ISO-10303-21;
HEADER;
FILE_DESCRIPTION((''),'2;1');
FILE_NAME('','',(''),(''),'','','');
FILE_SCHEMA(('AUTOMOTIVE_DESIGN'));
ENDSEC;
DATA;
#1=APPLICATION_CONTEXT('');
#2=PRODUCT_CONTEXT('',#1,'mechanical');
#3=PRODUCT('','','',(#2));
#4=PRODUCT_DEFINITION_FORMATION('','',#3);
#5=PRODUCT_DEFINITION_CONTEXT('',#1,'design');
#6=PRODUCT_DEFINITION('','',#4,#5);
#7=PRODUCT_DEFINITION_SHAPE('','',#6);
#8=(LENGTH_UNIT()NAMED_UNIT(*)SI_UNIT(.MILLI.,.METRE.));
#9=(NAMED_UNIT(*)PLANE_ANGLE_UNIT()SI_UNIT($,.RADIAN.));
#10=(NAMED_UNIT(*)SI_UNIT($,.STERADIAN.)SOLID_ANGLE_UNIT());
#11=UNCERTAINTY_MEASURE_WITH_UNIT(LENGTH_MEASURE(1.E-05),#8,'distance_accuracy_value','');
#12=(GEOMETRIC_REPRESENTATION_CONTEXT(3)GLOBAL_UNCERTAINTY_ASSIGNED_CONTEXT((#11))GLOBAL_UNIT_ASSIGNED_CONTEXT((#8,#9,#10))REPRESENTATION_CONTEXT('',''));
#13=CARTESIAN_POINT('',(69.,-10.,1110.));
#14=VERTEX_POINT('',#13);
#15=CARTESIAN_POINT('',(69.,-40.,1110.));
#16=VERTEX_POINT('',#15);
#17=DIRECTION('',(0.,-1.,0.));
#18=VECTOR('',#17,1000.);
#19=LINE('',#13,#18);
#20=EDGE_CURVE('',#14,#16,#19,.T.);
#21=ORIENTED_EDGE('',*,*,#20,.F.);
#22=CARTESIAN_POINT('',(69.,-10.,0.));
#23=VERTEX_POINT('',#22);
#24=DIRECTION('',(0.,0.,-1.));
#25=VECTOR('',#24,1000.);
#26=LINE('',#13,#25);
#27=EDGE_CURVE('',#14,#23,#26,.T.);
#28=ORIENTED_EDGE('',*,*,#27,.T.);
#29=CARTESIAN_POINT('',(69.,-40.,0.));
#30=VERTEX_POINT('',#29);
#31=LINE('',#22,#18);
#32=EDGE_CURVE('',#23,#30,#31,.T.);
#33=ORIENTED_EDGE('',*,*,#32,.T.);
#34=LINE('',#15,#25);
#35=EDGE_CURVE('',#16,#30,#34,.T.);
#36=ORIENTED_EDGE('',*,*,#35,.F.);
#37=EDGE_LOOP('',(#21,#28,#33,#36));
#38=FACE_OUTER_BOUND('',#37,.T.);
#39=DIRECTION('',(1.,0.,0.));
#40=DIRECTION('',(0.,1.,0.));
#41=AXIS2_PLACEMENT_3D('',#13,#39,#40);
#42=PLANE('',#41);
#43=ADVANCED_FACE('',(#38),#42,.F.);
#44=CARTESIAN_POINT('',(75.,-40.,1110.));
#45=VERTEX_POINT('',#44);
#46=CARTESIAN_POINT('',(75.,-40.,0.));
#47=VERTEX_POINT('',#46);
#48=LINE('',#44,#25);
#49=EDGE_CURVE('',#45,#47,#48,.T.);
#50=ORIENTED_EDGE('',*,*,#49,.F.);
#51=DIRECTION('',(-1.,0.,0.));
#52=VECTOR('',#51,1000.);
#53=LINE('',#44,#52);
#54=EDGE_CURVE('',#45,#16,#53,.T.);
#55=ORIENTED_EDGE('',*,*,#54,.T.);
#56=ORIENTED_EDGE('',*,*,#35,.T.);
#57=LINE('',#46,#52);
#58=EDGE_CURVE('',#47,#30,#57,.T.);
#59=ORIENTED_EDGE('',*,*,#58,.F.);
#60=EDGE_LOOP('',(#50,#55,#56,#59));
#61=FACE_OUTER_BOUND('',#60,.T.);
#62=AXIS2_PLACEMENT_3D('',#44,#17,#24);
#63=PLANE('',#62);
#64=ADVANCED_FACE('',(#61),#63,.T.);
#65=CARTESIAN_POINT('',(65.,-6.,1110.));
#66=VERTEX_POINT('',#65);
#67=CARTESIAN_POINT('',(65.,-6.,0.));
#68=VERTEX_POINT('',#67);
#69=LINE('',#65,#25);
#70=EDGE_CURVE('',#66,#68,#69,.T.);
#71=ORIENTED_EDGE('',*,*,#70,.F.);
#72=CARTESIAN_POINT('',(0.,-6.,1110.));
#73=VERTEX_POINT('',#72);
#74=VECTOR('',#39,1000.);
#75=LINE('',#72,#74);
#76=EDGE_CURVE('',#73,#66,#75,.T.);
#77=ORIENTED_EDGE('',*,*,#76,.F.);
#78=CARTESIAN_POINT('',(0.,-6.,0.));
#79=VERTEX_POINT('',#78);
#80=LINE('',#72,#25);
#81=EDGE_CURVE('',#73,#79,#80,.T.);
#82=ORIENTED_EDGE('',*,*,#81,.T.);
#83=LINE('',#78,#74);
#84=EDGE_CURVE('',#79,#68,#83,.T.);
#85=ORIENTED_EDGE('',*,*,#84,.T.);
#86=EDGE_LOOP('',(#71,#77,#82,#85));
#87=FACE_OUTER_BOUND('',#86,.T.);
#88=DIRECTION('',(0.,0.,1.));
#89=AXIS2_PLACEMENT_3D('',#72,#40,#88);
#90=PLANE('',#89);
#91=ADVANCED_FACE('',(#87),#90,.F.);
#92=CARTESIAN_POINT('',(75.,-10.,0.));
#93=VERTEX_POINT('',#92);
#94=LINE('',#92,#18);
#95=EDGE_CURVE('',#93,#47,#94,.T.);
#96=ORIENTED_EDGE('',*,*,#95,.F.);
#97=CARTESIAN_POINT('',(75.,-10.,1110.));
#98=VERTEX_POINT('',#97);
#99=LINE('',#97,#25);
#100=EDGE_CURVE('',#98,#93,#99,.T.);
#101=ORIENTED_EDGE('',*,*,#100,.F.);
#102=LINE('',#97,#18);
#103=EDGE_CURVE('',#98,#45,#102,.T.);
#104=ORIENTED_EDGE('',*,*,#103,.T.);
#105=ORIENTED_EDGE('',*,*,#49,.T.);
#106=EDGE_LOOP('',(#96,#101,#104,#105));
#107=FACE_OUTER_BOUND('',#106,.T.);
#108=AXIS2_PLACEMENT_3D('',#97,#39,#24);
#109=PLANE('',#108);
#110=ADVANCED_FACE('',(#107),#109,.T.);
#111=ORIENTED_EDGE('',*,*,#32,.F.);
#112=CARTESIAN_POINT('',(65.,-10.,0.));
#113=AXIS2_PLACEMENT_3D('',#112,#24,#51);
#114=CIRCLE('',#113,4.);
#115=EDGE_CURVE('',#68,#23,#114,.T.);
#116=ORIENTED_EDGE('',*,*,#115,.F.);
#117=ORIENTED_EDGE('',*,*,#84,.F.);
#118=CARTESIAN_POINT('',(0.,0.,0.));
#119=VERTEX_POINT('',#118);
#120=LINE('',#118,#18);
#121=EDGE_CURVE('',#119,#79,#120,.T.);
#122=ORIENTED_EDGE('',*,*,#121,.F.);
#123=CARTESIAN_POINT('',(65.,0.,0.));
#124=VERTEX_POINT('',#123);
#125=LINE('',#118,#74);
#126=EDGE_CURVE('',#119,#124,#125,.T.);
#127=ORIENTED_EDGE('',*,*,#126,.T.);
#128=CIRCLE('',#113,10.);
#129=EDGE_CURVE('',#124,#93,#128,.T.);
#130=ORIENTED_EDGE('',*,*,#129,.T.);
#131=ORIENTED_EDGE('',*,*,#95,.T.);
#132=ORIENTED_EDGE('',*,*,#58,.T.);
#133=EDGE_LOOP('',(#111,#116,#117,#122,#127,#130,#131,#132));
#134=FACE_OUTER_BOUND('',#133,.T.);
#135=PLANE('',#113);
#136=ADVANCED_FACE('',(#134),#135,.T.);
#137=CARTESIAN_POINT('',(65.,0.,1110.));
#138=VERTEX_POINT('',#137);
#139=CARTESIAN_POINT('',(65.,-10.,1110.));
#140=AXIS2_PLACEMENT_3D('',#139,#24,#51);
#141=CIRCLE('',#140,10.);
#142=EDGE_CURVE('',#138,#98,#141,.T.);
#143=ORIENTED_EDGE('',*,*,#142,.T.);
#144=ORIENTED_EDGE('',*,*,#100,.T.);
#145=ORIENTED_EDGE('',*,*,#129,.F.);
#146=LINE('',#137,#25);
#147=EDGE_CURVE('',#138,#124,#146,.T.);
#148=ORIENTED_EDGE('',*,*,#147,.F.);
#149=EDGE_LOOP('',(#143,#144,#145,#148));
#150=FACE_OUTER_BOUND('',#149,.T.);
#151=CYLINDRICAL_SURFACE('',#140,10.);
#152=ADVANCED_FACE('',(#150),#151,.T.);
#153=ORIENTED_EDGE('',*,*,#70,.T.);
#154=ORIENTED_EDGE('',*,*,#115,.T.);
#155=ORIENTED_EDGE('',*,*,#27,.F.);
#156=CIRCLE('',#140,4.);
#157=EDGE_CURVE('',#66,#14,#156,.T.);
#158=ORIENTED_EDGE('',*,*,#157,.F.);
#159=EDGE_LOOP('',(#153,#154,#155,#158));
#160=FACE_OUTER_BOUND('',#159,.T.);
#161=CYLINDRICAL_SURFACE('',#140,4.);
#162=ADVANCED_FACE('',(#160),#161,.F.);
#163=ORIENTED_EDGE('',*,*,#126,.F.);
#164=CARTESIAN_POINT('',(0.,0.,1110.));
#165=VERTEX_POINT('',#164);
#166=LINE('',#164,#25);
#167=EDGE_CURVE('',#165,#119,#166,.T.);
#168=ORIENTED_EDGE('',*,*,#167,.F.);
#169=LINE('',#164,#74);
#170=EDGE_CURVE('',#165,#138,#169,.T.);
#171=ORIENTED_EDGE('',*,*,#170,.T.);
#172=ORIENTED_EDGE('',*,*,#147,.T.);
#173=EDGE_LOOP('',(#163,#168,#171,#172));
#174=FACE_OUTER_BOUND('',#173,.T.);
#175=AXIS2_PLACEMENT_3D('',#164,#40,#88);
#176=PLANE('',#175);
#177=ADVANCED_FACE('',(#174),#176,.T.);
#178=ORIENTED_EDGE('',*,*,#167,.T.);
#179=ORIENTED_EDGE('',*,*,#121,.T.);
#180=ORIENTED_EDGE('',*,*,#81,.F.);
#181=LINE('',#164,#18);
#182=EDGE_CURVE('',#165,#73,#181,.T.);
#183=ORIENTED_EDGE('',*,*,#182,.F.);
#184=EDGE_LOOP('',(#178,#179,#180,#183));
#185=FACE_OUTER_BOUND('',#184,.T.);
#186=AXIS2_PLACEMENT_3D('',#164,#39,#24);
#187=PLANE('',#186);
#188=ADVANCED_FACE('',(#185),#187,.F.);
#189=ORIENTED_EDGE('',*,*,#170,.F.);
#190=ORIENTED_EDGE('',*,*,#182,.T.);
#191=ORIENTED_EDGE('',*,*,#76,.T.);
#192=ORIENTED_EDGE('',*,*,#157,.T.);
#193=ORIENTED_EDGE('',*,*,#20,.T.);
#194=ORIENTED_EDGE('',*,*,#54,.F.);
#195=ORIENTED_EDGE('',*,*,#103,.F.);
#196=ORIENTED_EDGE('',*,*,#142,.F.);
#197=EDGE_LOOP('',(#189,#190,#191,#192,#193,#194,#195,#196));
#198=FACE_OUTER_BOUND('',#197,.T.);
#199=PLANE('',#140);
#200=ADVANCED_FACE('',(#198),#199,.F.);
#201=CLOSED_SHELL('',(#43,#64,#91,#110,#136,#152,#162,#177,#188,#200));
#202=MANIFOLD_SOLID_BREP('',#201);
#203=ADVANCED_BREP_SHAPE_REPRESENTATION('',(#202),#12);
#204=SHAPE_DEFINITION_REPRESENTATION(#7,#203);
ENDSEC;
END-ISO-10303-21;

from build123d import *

# Parameters (mm, degrees)
BOSS_EXTRUDE1_DEPTH = 1110


with BuildPart() as part:
    # Sketch1 → Boss-Extrude1 (new body)
    with BuildSketch(Plane.XY):
        with BuildLine():
            Line((0, 0), (65, 0))
            ThreePointArc((65, 0), (72.071067812, -2.928932188), (75, -10))
            Line((75, -10), (75, -40))
            Line((75, -40), (69, -40))
            Line((69, -40), (69, -10))
            ThreePointArc((69, -10), (67.828427125, -7.171572875), (65, -6))
            Line((65, -6), (0, -6))
            Line((0, -6), (0, 0))
        make_face()
    extrude(amount=BOSS_EXTRUDE1_DEPTH)


solid = part.part
